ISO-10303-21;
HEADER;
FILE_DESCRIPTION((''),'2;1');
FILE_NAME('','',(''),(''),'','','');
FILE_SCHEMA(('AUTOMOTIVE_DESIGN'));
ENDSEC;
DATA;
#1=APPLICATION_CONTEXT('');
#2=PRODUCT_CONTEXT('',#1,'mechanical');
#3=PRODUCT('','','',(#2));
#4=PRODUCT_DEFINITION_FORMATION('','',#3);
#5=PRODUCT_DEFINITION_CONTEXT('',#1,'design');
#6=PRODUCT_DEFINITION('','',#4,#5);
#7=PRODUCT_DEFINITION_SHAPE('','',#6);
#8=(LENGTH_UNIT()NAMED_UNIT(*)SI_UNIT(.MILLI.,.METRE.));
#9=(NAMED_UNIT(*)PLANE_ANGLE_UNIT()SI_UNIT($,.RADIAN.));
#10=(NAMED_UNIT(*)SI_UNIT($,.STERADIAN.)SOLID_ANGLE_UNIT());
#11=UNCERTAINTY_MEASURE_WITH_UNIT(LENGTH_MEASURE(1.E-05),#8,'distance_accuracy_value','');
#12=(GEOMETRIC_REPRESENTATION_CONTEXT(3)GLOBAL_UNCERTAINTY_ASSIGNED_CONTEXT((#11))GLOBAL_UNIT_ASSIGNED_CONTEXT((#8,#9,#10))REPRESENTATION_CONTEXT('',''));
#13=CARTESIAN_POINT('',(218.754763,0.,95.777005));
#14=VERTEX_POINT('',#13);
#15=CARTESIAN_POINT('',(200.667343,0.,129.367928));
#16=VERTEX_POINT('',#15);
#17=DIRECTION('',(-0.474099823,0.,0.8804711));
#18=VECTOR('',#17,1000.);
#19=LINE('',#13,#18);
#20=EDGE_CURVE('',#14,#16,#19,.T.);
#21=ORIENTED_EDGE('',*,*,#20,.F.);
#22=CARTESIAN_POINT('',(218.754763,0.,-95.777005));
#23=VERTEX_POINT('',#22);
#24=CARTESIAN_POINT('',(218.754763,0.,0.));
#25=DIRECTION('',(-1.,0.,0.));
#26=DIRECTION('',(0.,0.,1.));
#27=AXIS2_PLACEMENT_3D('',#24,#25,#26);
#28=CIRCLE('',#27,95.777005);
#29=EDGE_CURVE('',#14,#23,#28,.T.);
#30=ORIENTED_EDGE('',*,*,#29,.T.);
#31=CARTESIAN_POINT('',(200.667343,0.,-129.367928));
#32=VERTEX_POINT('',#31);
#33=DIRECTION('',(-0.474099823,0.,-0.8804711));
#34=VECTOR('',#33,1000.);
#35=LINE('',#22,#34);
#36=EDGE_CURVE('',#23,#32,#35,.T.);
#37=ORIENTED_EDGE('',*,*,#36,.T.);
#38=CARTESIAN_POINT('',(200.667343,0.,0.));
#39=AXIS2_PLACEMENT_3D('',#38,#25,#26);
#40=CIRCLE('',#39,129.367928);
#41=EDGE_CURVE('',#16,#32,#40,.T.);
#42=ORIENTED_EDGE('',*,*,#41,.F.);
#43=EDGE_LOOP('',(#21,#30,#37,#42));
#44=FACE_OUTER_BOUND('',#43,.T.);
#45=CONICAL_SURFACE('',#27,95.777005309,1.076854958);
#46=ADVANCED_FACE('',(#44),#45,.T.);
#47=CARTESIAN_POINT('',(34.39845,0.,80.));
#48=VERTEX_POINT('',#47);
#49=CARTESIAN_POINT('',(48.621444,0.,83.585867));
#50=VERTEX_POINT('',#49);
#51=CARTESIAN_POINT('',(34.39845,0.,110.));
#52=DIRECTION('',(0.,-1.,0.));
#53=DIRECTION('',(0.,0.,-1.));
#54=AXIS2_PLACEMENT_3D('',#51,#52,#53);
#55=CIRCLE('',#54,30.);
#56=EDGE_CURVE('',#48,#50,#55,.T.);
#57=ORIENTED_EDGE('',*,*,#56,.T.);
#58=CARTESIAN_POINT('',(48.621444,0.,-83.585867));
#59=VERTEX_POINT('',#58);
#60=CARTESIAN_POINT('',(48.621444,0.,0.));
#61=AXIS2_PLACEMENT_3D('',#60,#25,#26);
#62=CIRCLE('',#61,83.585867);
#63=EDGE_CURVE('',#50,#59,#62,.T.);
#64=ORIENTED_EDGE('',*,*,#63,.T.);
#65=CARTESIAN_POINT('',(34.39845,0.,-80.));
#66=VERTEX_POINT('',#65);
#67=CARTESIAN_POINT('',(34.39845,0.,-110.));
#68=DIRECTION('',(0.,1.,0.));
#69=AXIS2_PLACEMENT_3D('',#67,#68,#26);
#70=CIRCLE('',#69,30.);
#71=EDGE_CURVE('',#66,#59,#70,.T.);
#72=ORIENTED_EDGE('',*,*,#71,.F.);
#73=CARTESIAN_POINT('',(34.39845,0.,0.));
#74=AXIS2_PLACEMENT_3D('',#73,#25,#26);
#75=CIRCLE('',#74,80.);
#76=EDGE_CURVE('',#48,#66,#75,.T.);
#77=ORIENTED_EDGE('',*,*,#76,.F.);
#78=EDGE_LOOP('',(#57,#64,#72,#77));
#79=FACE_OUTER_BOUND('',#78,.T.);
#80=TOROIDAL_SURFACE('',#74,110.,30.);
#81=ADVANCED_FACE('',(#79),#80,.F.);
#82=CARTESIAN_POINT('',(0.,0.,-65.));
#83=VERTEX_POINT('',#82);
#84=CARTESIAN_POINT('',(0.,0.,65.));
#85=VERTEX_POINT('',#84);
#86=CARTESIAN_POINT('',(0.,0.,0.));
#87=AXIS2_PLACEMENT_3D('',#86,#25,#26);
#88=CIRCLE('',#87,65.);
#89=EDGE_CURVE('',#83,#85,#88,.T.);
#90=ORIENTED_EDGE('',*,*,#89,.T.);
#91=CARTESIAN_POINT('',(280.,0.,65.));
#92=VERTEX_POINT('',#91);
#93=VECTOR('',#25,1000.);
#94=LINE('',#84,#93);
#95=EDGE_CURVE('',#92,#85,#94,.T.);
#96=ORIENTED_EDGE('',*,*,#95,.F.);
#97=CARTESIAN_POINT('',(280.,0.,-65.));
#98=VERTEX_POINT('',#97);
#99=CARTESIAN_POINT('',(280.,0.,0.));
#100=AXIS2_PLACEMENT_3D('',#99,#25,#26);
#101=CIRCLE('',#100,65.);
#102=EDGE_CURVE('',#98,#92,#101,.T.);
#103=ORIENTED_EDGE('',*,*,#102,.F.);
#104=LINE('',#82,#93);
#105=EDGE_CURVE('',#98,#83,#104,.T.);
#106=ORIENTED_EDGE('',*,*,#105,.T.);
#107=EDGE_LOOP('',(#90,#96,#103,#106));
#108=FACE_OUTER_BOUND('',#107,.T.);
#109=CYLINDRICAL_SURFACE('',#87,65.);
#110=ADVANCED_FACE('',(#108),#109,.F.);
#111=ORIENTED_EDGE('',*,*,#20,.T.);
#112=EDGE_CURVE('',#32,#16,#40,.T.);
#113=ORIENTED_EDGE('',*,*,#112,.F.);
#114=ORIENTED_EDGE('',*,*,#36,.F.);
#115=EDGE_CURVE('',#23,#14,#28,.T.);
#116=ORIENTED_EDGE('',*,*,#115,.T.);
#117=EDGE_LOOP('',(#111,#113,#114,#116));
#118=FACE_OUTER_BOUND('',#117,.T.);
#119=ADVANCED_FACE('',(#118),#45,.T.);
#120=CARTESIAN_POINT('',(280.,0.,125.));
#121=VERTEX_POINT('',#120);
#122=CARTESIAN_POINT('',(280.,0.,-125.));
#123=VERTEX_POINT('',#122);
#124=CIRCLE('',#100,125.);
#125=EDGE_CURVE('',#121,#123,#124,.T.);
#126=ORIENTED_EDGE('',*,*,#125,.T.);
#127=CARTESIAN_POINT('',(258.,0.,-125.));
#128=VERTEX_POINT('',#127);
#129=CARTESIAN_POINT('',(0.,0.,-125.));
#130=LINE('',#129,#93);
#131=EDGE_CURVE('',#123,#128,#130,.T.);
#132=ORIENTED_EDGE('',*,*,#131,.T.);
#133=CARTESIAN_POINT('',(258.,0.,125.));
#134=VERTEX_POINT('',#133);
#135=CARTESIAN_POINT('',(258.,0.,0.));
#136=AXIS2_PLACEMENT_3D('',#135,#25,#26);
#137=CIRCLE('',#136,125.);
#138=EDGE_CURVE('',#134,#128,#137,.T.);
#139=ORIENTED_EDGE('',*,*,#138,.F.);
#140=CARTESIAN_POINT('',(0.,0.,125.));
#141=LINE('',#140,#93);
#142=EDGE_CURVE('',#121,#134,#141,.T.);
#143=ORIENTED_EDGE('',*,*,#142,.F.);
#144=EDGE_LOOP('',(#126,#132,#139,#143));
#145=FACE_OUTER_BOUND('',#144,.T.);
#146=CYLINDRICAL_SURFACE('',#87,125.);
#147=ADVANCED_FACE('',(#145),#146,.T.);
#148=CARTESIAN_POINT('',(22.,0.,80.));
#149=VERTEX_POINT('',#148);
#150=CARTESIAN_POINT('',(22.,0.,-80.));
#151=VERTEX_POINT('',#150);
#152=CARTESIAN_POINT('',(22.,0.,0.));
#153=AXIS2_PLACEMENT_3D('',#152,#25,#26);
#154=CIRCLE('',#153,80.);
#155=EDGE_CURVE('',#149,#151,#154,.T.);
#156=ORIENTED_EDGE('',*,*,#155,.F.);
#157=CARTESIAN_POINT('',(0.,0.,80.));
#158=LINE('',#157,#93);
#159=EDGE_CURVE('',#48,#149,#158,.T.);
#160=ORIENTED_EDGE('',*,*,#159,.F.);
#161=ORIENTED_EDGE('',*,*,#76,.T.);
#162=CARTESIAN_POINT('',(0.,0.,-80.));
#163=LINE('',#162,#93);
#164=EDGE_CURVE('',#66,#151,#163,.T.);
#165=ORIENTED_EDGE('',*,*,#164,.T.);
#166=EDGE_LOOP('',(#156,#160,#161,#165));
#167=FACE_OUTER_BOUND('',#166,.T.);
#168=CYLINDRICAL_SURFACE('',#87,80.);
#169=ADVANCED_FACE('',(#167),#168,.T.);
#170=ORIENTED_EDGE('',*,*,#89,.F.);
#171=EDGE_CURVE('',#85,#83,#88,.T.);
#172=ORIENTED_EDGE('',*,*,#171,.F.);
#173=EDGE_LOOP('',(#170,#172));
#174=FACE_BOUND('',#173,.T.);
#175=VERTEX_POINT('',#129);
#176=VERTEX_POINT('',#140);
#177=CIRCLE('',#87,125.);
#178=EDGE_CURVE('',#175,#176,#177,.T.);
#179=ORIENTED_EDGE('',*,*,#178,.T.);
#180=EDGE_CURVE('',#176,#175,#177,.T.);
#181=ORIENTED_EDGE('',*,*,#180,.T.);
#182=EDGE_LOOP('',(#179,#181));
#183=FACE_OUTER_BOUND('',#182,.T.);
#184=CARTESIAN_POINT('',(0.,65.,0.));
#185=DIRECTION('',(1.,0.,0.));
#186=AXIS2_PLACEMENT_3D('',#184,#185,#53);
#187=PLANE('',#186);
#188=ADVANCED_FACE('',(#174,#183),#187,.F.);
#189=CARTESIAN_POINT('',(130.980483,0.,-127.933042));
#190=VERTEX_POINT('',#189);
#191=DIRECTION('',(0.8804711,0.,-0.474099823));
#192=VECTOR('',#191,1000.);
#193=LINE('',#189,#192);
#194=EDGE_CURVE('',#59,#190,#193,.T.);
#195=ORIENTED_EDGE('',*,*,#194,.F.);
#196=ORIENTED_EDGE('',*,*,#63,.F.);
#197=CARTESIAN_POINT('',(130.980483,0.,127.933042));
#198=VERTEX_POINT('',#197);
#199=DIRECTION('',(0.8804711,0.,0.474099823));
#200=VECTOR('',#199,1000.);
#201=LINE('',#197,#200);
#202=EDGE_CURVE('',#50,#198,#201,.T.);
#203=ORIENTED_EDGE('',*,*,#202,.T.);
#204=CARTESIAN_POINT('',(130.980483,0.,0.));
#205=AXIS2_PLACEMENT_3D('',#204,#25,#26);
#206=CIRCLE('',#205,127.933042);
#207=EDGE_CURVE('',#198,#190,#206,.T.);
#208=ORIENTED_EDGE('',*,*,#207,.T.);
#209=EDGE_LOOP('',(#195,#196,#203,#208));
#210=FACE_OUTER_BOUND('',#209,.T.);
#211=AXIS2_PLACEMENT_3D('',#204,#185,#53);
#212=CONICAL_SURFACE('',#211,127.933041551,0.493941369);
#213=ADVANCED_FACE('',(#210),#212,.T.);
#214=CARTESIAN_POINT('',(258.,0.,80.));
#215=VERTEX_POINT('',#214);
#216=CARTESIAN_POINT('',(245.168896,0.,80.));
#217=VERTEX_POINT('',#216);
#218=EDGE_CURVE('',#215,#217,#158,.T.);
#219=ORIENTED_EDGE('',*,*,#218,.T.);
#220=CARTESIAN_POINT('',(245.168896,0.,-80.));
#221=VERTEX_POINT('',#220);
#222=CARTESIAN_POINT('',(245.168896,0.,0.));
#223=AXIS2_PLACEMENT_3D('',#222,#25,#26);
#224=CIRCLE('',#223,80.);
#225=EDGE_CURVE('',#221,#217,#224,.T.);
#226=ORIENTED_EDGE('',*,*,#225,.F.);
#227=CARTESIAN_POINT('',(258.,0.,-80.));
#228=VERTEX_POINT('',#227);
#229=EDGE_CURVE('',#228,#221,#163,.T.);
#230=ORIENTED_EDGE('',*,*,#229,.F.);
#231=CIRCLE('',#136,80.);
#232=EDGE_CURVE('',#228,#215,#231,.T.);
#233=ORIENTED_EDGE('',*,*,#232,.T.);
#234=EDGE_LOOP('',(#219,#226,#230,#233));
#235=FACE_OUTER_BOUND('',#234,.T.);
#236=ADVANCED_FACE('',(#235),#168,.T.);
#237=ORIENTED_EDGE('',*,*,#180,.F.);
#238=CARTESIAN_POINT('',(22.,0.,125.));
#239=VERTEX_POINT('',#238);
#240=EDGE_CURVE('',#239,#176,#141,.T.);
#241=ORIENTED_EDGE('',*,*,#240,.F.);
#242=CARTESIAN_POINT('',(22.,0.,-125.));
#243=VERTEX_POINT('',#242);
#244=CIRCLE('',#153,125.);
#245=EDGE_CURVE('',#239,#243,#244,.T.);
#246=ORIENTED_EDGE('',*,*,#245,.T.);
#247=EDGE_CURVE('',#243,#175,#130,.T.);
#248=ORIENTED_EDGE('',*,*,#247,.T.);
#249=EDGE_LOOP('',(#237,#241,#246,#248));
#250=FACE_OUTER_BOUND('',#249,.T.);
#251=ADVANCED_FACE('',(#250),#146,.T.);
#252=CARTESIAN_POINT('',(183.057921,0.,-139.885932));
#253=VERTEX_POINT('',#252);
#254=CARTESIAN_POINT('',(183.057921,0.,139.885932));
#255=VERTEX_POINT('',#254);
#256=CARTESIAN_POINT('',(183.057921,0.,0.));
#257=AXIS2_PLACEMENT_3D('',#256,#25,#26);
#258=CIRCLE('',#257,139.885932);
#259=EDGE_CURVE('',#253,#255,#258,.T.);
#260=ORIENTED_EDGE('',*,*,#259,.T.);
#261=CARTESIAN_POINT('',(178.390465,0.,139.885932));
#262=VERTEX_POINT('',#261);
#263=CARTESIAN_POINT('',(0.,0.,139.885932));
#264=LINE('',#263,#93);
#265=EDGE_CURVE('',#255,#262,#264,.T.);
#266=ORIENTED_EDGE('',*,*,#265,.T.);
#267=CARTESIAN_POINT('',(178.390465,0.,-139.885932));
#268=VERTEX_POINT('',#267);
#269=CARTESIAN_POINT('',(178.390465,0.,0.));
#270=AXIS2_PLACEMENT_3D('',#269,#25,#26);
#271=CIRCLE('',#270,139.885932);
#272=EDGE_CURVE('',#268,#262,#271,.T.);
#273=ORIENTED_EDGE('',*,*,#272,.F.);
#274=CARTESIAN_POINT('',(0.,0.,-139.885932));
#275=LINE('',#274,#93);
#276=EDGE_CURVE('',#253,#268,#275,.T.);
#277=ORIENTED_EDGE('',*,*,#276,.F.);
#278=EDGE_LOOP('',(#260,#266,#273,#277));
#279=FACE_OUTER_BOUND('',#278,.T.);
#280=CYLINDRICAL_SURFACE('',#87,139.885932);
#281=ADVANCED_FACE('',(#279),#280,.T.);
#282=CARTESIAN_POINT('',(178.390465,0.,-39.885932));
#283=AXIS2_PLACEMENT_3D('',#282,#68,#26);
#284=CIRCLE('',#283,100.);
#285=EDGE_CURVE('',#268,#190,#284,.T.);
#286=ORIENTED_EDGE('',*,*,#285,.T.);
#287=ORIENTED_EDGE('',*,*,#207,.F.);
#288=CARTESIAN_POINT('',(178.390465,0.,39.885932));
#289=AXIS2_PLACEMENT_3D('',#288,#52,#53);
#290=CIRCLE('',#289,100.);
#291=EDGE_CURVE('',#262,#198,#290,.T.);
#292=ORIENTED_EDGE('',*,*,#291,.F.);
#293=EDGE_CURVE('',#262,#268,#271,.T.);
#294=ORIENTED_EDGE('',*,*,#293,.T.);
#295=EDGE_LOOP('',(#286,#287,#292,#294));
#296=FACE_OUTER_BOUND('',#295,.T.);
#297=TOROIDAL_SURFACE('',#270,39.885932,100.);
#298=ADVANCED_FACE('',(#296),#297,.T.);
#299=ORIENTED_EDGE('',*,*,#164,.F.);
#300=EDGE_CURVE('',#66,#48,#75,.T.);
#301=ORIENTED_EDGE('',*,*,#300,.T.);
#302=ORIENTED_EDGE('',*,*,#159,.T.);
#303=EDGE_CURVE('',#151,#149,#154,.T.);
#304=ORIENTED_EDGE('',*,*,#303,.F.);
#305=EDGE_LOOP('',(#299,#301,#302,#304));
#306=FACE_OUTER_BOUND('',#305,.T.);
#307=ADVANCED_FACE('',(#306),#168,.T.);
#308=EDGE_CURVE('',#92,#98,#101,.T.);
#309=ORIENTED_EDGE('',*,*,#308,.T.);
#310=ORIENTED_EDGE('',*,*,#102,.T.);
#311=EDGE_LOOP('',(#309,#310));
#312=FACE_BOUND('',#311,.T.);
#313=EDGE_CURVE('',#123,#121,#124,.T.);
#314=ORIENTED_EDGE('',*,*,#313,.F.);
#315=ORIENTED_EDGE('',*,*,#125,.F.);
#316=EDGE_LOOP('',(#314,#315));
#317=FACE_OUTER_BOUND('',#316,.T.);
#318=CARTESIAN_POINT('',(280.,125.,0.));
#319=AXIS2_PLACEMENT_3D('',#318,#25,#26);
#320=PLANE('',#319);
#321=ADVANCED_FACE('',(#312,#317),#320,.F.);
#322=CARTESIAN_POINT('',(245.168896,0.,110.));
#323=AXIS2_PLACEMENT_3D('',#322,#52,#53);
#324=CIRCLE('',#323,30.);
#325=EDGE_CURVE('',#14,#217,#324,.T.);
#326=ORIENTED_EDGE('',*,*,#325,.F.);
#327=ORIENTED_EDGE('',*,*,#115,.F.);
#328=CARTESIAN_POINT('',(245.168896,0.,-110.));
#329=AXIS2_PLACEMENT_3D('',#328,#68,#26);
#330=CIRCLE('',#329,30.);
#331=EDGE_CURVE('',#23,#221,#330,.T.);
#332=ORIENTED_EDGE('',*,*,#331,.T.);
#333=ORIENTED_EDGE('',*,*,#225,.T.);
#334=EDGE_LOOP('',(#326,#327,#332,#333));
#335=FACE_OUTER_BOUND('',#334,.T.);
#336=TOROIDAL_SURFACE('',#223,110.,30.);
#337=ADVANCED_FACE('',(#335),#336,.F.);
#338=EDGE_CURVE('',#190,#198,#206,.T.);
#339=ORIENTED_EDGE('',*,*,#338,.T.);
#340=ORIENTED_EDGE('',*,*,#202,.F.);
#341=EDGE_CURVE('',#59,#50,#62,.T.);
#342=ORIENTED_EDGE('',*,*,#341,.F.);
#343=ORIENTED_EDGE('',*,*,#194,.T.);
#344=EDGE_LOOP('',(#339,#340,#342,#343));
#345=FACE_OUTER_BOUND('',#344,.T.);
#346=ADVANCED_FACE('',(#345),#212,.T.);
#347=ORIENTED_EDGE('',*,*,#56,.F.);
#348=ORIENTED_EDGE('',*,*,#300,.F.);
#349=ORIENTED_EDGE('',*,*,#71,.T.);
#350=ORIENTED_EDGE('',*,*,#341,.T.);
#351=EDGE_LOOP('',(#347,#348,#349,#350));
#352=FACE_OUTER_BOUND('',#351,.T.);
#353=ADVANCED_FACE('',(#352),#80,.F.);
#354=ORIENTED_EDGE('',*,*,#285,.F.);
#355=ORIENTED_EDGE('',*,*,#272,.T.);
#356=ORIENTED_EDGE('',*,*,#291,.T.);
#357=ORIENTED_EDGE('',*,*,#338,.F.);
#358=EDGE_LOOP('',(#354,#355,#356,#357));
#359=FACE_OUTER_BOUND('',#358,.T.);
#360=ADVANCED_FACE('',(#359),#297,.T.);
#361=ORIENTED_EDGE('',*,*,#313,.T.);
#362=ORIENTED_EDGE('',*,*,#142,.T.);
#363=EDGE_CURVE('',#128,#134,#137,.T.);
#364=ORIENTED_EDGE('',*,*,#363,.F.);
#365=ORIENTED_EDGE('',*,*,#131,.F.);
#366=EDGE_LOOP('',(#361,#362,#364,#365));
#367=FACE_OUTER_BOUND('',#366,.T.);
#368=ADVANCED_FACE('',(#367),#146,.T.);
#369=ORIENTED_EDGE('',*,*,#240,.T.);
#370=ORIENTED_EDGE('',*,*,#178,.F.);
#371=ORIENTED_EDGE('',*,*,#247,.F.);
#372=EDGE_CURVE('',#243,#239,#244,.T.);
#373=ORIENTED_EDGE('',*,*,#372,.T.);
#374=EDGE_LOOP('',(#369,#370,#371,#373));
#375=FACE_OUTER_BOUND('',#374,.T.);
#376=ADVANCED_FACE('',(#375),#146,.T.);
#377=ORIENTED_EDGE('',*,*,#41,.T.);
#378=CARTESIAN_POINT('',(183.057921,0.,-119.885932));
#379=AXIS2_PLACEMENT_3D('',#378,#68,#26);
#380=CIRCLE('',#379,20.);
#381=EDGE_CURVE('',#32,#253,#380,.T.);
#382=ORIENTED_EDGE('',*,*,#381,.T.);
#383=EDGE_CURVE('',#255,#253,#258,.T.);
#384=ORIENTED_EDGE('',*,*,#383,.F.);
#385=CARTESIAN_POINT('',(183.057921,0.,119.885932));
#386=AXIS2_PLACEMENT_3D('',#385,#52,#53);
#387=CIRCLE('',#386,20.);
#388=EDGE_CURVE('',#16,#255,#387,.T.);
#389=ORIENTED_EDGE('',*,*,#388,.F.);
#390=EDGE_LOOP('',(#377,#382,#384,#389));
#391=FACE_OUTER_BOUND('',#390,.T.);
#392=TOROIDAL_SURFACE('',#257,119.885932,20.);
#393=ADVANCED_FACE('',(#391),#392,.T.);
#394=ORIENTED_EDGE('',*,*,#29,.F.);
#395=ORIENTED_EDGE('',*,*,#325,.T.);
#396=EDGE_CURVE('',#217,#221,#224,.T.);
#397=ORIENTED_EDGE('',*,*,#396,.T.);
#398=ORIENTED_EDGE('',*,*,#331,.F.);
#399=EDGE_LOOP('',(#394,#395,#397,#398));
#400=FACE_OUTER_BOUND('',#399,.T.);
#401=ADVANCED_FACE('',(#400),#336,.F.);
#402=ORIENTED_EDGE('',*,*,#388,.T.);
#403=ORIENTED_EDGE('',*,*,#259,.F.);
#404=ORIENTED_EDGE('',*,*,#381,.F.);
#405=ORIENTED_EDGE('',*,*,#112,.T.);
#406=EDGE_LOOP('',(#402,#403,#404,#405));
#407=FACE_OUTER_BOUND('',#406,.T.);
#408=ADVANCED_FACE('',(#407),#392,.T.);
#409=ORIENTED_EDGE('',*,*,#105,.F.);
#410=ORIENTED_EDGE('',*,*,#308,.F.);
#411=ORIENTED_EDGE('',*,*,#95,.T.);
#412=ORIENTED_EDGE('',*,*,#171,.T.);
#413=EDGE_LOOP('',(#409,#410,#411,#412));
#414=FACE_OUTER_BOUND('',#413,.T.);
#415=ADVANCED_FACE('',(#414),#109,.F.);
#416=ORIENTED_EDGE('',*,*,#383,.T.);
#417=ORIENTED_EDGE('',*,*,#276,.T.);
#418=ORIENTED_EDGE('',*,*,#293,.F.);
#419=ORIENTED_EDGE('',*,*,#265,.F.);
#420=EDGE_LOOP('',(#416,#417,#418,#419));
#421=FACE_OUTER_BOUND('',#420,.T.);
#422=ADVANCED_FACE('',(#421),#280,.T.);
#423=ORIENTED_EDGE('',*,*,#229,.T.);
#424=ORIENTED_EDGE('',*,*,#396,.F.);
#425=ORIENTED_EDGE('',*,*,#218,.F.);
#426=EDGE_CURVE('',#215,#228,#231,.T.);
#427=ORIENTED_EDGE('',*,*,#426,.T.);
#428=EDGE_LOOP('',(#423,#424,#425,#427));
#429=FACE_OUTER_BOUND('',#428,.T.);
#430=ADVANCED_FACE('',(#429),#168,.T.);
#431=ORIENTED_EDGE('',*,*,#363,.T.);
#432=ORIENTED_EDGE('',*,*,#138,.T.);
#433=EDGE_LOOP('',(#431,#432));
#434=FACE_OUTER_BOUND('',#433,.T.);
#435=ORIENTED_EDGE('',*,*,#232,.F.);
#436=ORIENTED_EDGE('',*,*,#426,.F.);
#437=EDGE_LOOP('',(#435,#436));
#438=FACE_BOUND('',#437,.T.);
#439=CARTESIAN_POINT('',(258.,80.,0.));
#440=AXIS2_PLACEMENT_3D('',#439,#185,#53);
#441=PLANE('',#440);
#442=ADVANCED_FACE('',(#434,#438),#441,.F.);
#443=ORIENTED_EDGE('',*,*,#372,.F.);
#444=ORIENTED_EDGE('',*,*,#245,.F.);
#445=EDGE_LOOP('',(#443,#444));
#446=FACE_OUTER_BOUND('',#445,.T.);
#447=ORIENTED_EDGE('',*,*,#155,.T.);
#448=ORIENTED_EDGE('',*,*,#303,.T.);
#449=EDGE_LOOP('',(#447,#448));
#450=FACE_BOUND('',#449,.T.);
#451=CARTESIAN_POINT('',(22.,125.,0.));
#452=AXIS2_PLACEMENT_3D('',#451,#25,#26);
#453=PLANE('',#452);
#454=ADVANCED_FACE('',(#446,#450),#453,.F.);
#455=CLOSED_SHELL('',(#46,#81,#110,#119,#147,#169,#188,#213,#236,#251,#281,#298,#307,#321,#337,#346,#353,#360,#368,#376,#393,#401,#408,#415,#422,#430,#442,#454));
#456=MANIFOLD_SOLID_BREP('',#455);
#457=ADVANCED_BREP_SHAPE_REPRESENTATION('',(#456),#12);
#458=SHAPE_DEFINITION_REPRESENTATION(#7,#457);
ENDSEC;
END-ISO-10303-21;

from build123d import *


with BuildPart() as part:
    # Sketch1 → Revolve1 (revolve)
    with BuildSketch(Plane.XY, mode=Mode.PRIVATE) as revolve1_sk:
        with BuildLine():
            Line((0, 65), (0, 125))
            Line((0, 125), (22, 125))
            Line((22, 125), (22, 80))
            Line((22, 80), (34.398449785, 80))
            ThreePointArc((34.398449785, 80), (41.732480398, 80.910276815), (48.621444476, 83.585867002))
            Line((48.621444476, 83.585867002), (130.980482924, 127.933041551))
            ThreePointArc((130.980482924, 127.933041551), (153.943696517, 136.851675508), (178.390465228, 139.885931559))
            Line((178.390465228, 139.885931559), (183.05792065, 139.885931559))
            ThreePointArc((183.05792065, 139.885931559), (193.313652481, 137.056253763), (200.667342649, 129.36792802))
            Line((200.667342649, 129.36792802), (218.75476257, 95.777005309))
            ThreePointArc((218.75476257, 95.777005309), (229.785297821, 84.244516693), (245.168895567, 80))
            Line((245.168895567, 80), (258, 80))
            Line((258, 80), (258, 125))
            Line((258, 125), (280, 125))
            Line((280, 125), (280, 65))
            Line((280, 65), (0, 65))
        make_face()
    revolve(revolve1_sk.sketch.rotate(Axis((0, 0, 0), (1, 0, 0)), 90), axis=Axis((0, 0, 0), (1, 0, 0)))


solid = part.part
